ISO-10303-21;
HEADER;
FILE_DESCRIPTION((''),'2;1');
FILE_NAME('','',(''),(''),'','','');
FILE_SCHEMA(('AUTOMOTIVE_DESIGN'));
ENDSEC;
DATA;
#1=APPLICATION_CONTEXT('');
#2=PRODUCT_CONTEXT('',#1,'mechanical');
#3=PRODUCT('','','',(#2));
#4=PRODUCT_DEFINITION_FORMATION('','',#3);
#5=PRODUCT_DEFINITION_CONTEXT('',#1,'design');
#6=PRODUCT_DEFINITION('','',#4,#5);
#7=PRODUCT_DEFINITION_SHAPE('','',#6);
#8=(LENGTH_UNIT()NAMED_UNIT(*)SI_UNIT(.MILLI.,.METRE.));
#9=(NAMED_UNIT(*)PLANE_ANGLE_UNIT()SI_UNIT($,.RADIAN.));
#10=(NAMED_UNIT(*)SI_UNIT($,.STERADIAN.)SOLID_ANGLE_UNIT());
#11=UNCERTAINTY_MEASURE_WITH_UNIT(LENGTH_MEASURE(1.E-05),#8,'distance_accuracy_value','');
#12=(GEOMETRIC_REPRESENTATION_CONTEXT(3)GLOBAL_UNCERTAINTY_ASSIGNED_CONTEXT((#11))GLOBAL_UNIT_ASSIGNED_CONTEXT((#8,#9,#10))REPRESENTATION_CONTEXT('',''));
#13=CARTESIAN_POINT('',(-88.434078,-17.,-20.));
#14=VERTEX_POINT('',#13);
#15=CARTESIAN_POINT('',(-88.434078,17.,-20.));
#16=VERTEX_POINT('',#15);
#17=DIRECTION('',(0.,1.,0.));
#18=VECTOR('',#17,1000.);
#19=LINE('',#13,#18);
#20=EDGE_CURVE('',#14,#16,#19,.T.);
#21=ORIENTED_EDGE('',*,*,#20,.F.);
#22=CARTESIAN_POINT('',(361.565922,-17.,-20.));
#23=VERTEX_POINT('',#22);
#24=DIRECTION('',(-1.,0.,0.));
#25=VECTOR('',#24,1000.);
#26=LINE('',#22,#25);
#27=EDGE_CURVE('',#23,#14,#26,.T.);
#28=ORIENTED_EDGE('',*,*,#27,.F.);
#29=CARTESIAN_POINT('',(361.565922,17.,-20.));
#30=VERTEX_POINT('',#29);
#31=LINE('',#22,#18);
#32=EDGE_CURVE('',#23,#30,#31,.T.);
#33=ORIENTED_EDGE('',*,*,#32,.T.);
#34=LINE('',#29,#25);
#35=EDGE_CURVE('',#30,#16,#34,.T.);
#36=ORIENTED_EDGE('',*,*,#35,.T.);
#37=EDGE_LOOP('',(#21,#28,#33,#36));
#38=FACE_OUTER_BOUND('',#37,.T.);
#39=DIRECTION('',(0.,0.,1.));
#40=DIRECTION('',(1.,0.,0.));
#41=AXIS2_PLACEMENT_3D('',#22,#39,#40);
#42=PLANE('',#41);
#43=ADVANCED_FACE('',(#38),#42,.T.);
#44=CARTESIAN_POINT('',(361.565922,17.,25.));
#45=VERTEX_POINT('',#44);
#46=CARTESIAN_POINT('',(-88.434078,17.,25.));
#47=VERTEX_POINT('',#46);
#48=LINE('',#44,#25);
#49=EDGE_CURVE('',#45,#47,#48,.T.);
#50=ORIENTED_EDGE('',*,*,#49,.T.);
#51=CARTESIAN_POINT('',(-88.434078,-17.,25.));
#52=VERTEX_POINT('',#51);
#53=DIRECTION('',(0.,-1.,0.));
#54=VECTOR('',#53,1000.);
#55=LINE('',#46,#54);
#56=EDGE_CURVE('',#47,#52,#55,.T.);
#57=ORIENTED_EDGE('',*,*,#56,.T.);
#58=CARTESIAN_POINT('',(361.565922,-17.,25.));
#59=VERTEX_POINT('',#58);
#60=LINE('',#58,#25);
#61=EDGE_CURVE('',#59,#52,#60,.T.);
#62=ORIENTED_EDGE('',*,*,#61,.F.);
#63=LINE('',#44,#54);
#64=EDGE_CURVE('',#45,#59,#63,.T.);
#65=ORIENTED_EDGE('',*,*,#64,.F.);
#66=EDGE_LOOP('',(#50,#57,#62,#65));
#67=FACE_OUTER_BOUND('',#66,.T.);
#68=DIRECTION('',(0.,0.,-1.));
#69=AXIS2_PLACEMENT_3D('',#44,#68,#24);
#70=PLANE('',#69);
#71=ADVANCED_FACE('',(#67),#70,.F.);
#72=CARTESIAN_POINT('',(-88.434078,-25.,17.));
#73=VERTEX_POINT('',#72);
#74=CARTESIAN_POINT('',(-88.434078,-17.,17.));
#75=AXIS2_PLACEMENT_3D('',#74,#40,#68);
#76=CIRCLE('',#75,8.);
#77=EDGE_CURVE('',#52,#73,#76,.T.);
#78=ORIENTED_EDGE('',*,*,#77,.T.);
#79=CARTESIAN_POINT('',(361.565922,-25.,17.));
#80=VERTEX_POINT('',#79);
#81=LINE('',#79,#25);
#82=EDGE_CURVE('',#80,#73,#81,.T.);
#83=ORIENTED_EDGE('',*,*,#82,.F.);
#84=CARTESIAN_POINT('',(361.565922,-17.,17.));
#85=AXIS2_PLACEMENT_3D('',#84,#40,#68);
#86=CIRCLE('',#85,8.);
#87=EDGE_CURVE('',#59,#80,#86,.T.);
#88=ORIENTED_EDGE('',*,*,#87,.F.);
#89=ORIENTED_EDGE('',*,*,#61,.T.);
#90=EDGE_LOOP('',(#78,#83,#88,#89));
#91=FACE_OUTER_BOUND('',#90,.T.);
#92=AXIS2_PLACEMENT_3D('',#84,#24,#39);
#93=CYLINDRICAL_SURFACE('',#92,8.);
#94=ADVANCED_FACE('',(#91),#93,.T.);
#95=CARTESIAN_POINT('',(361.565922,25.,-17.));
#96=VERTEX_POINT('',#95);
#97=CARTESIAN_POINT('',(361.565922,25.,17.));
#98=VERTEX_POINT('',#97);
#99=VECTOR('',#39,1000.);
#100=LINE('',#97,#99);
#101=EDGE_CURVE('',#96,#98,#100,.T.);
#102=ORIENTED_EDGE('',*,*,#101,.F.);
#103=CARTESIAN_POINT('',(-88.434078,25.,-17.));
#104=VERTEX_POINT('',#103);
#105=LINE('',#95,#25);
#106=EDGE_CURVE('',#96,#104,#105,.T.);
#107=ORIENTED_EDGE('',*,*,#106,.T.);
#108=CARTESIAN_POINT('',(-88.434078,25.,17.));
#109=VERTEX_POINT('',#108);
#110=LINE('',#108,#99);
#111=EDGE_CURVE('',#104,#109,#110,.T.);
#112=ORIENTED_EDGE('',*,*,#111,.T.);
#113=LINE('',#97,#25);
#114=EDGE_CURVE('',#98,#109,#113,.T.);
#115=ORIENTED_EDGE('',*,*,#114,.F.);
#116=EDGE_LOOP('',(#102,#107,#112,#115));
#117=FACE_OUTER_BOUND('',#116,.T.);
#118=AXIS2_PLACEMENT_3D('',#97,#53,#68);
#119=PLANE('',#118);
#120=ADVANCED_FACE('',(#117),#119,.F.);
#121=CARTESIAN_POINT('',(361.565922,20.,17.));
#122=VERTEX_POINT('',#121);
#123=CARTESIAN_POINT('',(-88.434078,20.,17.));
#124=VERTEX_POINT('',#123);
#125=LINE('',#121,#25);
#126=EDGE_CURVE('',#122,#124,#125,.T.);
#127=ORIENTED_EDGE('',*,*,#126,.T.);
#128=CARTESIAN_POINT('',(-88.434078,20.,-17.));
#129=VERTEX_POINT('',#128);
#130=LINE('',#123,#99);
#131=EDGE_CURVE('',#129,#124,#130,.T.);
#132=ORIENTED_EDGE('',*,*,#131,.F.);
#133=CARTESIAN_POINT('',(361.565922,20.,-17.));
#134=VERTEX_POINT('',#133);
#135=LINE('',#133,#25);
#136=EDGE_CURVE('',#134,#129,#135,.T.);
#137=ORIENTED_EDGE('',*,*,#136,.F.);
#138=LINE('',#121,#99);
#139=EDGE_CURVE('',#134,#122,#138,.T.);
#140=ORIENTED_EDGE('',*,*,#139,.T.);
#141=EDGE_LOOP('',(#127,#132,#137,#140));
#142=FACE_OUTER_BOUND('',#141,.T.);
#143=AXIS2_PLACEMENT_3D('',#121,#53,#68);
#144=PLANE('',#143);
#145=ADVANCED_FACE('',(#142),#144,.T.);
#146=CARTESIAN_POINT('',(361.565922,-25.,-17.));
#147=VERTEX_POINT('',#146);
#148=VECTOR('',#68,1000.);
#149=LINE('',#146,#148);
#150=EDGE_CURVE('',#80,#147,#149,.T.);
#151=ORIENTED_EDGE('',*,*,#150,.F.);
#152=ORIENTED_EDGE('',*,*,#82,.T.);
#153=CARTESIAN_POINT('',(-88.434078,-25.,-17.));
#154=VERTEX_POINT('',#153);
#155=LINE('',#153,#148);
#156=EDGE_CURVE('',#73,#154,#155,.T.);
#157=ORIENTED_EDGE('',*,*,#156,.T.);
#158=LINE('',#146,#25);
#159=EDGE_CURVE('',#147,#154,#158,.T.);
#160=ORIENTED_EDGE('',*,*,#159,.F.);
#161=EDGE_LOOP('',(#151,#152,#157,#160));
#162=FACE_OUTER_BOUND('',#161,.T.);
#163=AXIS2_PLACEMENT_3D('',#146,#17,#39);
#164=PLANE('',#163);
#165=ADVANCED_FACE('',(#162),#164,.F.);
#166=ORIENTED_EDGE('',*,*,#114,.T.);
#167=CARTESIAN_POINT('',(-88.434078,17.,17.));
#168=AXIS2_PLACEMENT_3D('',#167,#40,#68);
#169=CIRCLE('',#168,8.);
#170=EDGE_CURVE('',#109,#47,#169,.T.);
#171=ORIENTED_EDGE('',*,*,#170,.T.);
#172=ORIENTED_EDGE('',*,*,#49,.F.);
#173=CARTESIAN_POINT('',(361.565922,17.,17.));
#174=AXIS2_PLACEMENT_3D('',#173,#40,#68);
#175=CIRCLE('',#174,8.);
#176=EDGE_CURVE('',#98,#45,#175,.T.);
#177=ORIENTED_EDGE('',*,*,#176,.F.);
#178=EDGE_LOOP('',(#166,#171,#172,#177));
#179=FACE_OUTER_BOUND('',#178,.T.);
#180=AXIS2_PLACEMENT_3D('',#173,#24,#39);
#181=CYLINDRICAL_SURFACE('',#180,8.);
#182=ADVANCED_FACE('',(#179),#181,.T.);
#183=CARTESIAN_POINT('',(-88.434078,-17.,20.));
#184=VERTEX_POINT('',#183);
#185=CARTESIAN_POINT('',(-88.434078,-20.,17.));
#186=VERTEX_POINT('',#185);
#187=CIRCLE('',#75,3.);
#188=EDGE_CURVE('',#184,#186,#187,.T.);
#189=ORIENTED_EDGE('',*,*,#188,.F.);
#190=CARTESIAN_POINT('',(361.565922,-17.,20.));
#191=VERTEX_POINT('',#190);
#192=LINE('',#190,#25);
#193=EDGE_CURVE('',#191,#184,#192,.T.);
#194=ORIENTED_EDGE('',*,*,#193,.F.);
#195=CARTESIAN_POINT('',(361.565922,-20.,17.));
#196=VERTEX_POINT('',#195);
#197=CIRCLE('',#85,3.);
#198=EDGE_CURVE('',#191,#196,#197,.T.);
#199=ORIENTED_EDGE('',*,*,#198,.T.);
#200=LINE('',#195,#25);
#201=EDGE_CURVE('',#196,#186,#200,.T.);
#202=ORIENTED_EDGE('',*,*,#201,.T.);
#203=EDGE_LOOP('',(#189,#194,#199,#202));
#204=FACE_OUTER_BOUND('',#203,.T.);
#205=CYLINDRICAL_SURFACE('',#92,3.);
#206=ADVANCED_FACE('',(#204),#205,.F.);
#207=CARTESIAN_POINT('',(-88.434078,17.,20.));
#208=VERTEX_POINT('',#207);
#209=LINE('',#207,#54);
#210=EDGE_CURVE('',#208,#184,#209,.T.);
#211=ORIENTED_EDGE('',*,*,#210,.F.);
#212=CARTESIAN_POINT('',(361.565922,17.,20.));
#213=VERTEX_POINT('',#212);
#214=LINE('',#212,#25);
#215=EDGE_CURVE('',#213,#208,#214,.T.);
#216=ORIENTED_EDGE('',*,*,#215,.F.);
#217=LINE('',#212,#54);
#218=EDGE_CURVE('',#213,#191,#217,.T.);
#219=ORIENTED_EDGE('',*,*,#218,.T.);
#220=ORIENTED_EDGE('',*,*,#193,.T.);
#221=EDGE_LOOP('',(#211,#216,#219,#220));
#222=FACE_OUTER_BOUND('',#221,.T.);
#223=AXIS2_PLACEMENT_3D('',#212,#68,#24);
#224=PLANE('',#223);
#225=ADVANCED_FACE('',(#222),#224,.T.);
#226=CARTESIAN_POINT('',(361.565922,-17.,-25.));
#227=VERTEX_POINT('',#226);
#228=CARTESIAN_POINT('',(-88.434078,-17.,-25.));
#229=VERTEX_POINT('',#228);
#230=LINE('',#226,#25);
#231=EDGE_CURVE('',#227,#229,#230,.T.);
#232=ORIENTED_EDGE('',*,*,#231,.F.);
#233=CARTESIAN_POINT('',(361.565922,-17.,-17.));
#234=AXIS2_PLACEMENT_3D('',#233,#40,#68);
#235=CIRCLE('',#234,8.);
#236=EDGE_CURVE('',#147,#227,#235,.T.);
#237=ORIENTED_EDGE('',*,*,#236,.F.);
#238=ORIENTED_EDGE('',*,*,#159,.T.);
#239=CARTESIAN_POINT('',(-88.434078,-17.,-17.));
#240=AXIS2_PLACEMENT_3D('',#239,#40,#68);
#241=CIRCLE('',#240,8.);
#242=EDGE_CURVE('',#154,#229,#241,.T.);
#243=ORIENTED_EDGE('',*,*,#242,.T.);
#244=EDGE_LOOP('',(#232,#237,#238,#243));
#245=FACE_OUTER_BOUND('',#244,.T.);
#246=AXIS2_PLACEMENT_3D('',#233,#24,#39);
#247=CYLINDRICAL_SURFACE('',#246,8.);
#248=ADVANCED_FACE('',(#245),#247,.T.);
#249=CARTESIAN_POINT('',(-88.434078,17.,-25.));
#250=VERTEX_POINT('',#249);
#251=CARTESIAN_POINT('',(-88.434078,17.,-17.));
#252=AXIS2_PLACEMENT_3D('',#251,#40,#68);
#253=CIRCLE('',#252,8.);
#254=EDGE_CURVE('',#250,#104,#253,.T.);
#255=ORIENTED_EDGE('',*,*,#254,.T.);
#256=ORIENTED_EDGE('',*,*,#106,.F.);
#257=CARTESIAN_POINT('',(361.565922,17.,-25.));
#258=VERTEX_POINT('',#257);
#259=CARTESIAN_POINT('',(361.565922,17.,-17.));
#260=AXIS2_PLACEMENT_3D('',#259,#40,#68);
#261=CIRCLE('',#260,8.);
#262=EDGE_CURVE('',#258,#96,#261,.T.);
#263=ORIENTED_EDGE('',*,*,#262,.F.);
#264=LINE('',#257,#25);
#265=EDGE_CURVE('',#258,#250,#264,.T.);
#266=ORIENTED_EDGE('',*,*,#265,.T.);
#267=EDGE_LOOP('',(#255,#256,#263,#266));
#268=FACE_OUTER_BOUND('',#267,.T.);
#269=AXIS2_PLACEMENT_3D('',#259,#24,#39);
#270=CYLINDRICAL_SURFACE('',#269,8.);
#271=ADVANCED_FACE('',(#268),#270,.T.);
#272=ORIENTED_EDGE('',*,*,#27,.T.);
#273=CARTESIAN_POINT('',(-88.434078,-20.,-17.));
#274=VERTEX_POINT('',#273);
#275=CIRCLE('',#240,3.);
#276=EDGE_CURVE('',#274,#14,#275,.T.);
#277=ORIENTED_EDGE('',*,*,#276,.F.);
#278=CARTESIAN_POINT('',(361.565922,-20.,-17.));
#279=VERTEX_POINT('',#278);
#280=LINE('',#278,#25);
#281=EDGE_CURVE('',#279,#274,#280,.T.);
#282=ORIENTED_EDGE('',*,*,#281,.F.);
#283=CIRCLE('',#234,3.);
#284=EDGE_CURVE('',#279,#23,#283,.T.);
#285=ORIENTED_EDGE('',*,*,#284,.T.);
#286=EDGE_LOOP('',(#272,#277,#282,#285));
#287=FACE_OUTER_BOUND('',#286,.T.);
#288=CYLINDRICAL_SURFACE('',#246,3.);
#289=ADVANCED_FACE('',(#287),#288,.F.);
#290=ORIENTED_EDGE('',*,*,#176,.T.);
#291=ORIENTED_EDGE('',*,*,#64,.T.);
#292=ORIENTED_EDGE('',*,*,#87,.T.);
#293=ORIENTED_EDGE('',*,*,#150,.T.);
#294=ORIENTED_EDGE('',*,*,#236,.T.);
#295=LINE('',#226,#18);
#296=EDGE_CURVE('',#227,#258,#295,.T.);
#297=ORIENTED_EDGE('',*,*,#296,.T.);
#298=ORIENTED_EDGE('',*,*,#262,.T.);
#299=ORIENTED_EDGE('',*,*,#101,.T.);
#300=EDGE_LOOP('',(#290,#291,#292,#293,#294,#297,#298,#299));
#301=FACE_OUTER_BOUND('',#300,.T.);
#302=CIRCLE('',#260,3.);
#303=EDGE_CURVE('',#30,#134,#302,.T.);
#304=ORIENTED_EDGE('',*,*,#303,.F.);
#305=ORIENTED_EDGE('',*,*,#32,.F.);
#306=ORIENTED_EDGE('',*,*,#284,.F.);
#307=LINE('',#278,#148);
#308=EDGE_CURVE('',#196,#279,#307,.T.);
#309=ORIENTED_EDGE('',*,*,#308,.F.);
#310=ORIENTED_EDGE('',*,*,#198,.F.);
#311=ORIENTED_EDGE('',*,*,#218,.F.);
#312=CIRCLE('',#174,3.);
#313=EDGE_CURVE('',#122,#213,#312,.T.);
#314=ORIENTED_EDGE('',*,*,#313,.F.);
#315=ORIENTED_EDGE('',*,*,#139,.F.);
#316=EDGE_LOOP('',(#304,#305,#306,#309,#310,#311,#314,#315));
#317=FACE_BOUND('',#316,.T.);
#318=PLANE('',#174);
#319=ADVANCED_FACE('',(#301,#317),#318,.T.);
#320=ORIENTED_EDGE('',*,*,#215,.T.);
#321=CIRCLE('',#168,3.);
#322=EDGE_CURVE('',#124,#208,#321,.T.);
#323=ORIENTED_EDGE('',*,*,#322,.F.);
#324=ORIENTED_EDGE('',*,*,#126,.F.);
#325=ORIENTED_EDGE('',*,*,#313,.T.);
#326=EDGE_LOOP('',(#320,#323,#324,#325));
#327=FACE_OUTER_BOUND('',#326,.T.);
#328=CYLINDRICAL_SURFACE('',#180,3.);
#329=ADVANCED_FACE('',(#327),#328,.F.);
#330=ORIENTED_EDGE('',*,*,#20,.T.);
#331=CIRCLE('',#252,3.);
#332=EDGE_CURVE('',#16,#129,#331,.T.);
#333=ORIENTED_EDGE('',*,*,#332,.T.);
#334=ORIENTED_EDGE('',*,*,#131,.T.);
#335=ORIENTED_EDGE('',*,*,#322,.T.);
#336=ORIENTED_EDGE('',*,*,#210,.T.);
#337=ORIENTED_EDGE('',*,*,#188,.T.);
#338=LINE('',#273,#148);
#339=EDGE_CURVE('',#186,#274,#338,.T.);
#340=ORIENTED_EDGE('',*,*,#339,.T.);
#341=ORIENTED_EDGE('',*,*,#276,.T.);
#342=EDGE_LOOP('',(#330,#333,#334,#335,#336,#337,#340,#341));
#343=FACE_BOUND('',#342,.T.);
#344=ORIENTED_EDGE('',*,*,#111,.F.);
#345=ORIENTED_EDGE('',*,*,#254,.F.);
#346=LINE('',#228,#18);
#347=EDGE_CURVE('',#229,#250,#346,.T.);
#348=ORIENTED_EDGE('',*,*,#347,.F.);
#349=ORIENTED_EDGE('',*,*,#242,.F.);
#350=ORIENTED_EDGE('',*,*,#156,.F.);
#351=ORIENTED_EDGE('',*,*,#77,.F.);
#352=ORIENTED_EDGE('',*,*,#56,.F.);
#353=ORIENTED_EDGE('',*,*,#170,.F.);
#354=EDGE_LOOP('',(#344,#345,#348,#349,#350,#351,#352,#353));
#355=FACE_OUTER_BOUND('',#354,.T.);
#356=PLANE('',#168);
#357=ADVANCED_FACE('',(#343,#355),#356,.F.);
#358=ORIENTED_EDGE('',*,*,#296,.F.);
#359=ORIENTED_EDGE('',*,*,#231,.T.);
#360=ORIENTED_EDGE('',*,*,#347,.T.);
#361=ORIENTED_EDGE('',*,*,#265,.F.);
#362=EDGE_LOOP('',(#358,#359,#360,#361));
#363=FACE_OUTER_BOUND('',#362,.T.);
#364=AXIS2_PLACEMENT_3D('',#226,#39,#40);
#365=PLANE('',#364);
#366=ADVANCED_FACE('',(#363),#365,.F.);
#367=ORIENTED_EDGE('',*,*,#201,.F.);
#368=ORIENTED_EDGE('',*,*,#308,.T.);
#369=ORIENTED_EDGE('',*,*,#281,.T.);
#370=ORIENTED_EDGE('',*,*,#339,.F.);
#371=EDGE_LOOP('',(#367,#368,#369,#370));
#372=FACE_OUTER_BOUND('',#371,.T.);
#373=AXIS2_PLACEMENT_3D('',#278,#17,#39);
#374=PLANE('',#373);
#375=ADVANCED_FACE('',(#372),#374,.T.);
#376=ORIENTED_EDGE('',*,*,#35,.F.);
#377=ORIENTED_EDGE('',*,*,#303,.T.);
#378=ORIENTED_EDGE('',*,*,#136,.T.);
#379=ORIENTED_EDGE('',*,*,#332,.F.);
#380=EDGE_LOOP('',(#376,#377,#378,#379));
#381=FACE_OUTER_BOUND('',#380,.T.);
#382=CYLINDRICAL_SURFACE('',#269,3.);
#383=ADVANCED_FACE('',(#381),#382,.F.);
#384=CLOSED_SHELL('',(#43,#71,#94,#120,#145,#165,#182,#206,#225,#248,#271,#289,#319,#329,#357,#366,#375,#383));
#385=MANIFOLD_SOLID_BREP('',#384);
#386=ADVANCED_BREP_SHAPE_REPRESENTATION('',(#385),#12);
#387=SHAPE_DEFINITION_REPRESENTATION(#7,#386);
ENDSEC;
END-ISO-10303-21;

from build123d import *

# Parameters (mm, degrees)
COLD_FORMED_SQUARE_HOLLOW_SECTION_GB_T_6_DEPTH = 450


with BuildPart() as part:
    # Sketch1 → Cold-formed square hollow section GB/T 6728-2002 50 X 50 X 4(1) (new body)
    with BuildSketch(Plane.YZ.offset(-88.434077868)):
        with BuildLine():
            Line((-17, -25), (17, -25))
            ThreePointArc((17, -25), (22.656854249, -22.656854249), (25, -17))
            Line((25, -17), (25, 17))
            ThreePointArc((25, 17), (22.656854249, 22.656854249), (17, 25))
            Line((17, 25), (-17, 25))
            ThreePointArc((-17, 25), (-22.656854249, 22.656854249), (-25, 17))
            Line((-25, 17), (-25, -17))
            ThreePointArc((-25, -17), (-22.656854249, -22.656854249), (-17, -25))
        make_face()
        with BuildLine():
            Line((-17, -20), (17, -20))
            ThreePointArc((17, -20), (19.121320344, -19.121320344), (20, -17))
            Line((20, -17), (20, 17))
            ThreePointArc((20, 17), (19.121320344, 19.121320344), (17, 20))
            Line((17, 20), (-17, 20))
            ThreePointArc((-17, 20), (-19.121320344, 19.121320344), (-20, 17))
            Line((-20, 17), (-20, -17))
            ThreePointArc((-20, -17), (-19.121320344, -19.121320344), (-17, -20))
        make_face(mode=Mode.SUBTRACT)
    extrude(amount=COLD_FORMED_SQUARE_HOLLOW_SECTION_GB_T_6_DEPTH)


solid = part.part
